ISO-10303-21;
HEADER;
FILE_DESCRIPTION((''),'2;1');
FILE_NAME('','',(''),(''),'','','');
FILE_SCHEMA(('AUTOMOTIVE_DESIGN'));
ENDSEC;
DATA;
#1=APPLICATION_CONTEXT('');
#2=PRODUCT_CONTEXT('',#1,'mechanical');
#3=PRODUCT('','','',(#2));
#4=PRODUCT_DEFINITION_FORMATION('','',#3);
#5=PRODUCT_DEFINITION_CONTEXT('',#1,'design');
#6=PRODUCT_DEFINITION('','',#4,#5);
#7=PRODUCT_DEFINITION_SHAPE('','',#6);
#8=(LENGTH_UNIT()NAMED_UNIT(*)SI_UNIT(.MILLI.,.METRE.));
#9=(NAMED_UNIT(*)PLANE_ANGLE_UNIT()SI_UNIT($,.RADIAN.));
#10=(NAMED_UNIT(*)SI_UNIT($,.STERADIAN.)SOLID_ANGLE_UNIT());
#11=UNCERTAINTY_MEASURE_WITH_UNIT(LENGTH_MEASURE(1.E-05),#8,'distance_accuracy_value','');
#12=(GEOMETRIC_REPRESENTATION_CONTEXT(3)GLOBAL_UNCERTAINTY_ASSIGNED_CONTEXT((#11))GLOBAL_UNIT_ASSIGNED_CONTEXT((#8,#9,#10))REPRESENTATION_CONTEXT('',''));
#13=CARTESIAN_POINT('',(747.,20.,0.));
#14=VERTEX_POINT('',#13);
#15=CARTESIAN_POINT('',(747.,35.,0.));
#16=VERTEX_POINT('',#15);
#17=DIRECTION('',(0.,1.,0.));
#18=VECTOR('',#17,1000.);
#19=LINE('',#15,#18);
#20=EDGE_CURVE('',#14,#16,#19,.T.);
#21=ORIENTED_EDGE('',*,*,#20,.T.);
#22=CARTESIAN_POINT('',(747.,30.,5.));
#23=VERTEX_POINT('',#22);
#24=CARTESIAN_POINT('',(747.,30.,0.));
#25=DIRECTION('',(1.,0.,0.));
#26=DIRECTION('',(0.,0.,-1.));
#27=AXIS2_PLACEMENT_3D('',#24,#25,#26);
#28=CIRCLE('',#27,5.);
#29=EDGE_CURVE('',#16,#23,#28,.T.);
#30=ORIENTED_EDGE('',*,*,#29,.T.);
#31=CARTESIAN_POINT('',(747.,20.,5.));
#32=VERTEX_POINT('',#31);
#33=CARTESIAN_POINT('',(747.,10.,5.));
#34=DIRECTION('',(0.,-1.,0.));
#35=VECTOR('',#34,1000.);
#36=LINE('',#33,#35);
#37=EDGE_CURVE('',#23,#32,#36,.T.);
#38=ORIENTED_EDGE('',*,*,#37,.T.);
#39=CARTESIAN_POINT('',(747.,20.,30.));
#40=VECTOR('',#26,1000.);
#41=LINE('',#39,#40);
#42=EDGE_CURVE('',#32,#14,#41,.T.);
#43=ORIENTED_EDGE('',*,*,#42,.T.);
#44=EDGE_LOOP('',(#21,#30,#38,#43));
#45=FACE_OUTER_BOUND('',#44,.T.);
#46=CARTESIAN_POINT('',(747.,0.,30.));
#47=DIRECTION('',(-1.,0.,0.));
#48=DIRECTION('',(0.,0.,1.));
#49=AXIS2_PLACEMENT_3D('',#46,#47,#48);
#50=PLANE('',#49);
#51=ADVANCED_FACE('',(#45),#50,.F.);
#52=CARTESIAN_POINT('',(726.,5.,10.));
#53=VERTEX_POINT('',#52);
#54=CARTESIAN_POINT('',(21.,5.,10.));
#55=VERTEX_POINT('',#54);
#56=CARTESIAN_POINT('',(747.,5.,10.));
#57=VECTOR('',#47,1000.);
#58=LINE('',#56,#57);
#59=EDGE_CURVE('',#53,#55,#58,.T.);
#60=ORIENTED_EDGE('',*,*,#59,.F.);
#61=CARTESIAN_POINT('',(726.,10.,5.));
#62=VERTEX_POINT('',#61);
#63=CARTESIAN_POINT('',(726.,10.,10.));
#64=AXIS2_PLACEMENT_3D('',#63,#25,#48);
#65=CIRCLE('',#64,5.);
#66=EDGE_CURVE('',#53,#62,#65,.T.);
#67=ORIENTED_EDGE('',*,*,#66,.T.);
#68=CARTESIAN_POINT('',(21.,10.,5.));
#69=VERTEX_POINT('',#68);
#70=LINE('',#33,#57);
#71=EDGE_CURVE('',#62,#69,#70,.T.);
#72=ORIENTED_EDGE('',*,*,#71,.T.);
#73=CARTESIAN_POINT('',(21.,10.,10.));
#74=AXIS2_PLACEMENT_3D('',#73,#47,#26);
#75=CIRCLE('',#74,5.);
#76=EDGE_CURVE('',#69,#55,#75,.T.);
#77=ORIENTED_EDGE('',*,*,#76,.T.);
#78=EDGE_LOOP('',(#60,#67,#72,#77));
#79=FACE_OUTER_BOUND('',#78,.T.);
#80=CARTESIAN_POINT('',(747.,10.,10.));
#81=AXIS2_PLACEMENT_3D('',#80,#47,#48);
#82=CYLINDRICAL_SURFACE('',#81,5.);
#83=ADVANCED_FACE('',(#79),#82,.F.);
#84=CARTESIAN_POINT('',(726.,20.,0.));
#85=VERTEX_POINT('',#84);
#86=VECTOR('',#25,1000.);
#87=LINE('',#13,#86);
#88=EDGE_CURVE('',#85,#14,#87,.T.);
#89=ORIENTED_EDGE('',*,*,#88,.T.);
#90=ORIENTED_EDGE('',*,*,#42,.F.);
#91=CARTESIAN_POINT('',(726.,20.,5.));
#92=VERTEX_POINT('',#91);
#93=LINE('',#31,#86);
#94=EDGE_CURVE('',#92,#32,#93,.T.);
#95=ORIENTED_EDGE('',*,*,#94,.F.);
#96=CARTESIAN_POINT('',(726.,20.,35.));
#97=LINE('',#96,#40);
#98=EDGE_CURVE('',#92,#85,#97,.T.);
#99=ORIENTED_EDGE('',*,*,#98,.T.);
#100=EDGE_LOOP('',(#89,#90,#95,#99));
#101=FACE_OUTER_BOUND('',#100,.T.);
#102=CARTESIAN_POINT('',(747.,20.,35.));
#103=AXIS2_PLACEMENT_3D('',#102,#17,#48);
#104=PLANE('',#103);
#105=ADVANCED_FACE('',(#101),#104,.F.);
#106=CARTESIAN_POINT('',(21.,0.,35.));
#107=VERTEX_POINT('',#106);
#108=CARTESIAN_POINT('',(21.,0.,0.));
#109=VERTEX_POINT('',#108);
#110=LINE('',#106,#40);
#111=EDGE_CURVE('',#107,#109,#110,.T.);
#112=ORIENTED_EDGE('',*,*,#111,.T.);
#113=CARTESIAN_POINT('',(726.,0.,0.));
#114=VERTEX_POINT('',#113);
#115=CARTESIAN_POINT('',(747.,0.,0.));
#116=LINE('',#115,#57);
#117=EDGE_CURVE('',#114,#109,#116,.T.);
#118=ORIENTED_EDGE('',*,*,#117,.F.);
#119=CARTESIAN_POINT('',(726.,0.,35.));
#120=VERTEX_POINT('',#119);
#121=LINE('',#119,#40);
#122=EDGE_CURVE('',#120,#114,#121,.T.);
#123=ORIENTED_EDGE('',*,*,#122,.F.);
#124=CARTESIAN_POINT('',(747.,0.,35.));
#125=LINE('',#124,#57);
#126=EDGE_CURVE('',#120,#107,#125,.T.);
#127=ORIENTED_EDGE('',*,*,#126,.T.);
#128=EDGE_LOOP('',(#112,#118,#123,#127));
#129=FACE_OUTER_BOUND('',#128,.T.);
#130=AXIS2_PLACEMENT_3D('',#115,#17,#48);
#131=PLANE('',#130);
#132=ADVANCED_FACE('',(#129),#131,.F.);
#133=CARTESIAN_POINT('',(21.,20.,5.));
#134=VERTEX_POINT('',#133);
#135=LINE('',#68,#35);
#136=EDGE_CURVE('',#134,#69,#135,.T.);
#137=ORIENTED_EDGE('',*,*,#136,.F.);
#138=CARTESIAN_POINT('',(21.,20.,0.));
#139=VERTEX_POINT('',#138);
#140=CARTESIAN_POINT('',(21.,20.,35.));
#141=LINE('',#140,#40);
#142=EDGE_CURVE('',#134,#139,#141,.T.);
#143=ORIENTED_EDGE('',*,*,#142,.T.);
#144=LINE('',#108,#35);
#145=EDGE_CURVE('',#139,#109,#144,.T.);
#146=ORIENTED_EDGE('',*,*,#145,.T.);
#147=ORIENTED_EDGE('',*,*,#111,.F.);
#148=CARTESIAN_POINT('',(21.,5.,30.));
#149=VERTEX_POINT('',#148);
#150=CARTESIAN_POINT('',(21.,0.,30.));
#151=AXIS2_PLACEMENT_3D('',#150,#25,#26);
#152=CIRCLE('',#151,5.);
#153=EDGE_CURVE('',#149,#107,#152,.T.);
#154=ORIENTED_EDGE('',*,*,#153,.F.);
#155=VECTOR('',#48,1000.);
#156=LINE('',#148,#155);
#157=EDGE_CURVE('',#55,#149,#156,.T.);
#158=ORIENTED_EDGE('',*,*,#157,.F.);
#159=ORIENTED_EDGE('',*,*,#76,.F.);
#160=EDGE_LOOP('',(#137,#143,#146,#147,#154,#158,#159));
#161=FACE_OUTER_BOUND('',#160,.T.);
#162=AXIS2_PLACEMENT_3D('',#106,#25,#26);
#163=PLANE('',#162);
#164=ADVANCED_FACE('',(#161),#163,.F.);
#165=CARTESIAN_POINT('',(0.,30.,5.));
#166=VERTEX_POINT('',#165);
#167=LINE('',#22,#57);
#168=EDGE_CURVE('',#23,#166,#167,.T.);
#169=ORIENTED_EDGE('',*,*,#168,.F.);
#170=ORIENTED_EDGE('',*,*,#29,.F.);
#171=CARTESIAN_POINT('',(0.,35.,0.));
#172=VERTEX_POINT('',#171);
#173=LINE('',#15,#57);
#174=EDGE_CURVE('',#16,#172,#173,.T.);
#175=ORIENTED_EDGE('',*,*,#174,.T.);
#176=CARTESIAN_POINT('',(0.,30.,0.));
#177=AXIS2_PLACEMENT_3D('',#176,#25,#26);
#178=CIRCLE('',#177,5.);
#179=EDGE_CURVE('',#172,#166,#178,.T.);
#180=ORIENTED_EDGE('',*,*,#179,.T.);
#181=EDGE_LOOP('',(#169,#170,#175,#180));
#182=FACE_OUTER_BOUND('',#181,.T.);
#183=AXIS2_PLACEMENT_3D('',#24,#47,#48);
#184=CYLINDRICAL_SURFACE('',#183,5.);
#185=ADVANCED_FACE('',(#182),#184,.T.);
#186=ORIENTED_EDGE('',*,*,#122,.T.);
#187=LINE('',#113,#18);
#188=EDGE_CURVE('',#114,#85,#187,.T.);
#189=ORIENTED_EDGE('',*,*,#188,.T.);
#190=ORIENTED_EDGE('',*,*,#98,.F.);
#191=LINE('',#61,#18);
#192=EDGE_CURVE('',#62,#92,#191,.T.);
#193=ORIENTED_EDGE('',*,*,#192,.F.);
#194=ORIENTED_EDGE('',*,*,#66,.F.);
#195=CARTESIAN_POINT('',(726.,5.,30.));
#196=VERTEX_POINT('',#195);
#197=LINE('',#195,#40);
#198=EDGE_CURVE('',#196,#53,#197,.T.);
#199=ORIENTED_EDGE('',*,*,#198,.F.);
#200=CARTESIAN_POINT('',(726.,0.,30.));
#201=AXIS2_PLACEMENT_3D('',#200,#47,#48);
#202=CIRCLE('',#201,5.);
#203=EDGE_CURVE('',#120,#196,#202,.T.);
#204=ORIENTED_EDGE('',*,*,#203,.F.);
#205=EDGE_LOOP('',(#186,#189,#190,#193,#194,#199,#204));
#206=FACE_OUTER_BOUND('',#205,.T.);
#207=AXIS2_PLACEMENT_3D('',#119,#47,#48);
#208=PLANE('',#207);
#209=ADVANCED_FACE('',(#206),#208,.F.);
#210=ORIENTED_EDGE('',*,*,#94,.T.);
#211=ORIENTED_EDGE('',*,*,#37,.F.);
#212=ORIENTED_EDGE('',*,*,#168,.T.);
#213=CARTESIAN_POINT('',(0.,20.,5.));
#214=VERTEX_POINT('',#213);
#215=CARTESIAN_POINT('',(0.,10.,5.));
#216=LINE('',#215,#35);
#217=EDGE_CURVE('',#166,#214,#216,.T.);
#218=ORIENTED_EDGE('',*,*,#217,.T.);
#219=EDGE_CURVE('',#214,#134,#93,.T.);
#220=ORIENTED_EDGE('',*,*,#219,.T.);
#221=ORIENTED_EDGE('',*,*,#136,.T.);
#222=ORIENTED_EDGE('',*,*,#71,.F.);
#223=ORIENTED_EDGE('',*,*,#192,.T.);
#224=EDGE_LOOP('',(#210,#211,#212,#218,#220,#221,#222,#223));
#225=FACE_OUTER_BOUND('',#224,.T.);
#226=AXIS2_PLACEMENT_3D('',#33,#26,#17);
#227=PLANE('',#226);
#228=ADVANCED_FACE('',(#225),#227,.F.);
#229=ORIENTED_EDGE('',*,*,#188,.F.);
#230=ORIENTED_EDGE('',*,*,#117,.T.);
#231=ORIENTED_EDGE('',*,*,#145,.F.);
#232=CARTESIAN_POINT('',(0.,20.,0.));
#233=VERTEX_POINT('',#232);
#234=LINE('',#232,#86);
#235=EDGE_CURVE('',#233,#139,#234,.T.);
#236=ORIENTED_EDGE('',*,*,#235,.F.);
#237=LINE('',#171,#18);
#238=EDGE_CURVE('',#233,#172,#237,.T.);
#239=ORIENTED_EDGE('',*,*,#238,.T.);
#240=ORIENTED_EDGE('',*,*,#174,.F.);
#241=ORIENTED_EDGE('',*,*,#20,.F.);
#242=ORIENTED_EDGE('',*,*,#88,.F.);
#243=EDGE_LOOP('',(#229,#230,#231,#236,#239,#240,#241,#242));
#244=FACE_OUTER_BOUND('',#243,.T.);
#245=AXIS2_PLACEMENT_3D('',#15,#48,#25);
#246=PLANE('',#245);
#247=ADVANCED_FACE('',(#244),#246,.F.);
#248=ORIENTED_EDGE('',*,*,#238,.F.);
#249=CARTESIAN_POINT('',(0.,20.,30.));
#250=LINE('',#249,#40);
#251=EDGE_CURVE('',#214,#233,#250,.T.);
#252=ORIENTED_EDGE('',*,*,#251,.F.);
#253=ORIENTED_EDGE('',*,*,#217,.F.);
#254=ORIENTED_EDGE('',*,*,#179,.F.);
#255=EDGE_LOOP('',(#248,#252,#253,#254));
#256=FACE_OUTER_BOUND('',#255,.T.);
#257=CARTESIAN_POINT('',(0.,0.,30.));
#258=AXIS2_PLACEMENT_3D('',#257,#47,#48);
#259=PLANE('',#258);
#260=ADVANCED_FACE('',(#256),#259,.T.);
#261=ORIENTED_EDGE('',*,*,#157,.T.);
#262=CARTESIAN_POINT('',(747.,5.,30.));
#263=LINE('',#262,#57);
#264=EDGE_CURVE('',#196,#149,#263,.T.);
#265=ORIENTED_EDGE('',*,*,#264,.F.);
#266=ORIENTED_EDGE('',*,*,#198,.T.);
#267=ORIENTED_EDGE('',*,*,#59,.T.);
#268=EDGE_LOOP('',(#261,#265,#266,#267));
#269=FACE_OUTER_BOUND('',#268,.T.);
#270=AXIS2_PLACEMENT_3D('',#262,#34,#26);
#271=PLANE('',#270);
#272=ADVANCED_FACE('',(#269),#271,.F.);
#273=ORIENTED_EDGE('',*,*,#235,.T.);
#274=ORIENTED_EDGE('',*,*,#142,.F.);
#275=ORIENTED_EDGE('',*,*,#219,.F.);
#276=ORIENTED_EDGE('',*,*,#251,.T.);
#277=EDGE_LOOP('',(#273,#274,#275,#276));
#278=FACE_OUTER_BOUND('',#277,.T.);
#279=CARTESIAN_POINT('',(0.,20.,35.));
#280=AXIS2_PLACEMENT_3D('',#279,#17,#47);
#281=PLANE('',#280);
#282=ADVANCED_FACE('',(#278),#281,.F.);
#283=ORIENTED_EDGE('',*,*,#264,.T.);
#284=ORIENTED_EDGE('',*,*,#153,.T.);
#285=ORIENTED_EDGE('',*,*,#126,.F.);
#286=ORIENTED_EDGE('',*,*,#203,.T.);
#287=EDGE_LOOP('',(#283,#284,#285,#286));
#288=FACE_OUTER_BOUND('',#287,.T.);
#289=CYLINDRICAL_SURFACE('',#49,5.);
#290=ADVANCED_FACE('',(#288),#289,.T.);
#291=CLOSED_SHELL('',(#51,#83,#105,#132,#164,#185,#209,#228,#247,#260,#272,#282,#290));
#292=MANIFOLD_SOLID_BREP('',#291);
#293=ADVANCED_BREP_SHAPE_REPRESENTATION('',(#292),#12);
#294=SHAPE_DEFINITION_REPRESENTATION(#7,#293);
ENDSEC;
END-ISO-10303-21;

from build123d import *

# Parameters (mm, degrees)
ANGLE_IRON_35_X_35_X_5_1_DEPTH = 747
SKETCH2_W                      = 21
SKETCH2_H                      = 20
CUT_EXTRUDE1_DEPTH             = 749.638096813


with BuildPart() as part:
    # Sketch11 → Angle Iron 35 X 35 X 5(1) (new body)
    with BuildSketch(Plane.YZ):
        with BuildLine():
            Line((0, 0), (0, 35))
            ThreePointArc((0, 35), (3.535533906, 33.535533906), (5, 30))
            Line((5, 30), (5, 10))
            ThreePointArc((5, 10), (6.464466094, 6.464466094), (10, 5))
            Line((10, 5), (30, 5))
            ThreePointArc((30, 5), (33.535533906, 3.535533906), (35, 0))
            Line((35, 0), (0, 0))
        make_face()
    extrude(amount=ANGLE_IRON_35_X_35_X_5_1_DEPTH)

    # Sketch2 → Cut-Extrude1 (cut, through all)
    with BuildSketch(Plane(origin=(0, 0, 0), x_dir=(-1, 0, 0), z_dir=(0, 0, -1))):
        with Locations((-10.5, 10)):
            Rectangle(SKETCH2_W, SKETCH2_H)
        with Locations((-736.5, 10)):
            Rectangle(SKETCH2_W, SKETCH2_H)
    extrude(amount=-CUT_EXTRUDE1_DEPTH, mode=Mode.SUBTRACT)


solid = part.part
